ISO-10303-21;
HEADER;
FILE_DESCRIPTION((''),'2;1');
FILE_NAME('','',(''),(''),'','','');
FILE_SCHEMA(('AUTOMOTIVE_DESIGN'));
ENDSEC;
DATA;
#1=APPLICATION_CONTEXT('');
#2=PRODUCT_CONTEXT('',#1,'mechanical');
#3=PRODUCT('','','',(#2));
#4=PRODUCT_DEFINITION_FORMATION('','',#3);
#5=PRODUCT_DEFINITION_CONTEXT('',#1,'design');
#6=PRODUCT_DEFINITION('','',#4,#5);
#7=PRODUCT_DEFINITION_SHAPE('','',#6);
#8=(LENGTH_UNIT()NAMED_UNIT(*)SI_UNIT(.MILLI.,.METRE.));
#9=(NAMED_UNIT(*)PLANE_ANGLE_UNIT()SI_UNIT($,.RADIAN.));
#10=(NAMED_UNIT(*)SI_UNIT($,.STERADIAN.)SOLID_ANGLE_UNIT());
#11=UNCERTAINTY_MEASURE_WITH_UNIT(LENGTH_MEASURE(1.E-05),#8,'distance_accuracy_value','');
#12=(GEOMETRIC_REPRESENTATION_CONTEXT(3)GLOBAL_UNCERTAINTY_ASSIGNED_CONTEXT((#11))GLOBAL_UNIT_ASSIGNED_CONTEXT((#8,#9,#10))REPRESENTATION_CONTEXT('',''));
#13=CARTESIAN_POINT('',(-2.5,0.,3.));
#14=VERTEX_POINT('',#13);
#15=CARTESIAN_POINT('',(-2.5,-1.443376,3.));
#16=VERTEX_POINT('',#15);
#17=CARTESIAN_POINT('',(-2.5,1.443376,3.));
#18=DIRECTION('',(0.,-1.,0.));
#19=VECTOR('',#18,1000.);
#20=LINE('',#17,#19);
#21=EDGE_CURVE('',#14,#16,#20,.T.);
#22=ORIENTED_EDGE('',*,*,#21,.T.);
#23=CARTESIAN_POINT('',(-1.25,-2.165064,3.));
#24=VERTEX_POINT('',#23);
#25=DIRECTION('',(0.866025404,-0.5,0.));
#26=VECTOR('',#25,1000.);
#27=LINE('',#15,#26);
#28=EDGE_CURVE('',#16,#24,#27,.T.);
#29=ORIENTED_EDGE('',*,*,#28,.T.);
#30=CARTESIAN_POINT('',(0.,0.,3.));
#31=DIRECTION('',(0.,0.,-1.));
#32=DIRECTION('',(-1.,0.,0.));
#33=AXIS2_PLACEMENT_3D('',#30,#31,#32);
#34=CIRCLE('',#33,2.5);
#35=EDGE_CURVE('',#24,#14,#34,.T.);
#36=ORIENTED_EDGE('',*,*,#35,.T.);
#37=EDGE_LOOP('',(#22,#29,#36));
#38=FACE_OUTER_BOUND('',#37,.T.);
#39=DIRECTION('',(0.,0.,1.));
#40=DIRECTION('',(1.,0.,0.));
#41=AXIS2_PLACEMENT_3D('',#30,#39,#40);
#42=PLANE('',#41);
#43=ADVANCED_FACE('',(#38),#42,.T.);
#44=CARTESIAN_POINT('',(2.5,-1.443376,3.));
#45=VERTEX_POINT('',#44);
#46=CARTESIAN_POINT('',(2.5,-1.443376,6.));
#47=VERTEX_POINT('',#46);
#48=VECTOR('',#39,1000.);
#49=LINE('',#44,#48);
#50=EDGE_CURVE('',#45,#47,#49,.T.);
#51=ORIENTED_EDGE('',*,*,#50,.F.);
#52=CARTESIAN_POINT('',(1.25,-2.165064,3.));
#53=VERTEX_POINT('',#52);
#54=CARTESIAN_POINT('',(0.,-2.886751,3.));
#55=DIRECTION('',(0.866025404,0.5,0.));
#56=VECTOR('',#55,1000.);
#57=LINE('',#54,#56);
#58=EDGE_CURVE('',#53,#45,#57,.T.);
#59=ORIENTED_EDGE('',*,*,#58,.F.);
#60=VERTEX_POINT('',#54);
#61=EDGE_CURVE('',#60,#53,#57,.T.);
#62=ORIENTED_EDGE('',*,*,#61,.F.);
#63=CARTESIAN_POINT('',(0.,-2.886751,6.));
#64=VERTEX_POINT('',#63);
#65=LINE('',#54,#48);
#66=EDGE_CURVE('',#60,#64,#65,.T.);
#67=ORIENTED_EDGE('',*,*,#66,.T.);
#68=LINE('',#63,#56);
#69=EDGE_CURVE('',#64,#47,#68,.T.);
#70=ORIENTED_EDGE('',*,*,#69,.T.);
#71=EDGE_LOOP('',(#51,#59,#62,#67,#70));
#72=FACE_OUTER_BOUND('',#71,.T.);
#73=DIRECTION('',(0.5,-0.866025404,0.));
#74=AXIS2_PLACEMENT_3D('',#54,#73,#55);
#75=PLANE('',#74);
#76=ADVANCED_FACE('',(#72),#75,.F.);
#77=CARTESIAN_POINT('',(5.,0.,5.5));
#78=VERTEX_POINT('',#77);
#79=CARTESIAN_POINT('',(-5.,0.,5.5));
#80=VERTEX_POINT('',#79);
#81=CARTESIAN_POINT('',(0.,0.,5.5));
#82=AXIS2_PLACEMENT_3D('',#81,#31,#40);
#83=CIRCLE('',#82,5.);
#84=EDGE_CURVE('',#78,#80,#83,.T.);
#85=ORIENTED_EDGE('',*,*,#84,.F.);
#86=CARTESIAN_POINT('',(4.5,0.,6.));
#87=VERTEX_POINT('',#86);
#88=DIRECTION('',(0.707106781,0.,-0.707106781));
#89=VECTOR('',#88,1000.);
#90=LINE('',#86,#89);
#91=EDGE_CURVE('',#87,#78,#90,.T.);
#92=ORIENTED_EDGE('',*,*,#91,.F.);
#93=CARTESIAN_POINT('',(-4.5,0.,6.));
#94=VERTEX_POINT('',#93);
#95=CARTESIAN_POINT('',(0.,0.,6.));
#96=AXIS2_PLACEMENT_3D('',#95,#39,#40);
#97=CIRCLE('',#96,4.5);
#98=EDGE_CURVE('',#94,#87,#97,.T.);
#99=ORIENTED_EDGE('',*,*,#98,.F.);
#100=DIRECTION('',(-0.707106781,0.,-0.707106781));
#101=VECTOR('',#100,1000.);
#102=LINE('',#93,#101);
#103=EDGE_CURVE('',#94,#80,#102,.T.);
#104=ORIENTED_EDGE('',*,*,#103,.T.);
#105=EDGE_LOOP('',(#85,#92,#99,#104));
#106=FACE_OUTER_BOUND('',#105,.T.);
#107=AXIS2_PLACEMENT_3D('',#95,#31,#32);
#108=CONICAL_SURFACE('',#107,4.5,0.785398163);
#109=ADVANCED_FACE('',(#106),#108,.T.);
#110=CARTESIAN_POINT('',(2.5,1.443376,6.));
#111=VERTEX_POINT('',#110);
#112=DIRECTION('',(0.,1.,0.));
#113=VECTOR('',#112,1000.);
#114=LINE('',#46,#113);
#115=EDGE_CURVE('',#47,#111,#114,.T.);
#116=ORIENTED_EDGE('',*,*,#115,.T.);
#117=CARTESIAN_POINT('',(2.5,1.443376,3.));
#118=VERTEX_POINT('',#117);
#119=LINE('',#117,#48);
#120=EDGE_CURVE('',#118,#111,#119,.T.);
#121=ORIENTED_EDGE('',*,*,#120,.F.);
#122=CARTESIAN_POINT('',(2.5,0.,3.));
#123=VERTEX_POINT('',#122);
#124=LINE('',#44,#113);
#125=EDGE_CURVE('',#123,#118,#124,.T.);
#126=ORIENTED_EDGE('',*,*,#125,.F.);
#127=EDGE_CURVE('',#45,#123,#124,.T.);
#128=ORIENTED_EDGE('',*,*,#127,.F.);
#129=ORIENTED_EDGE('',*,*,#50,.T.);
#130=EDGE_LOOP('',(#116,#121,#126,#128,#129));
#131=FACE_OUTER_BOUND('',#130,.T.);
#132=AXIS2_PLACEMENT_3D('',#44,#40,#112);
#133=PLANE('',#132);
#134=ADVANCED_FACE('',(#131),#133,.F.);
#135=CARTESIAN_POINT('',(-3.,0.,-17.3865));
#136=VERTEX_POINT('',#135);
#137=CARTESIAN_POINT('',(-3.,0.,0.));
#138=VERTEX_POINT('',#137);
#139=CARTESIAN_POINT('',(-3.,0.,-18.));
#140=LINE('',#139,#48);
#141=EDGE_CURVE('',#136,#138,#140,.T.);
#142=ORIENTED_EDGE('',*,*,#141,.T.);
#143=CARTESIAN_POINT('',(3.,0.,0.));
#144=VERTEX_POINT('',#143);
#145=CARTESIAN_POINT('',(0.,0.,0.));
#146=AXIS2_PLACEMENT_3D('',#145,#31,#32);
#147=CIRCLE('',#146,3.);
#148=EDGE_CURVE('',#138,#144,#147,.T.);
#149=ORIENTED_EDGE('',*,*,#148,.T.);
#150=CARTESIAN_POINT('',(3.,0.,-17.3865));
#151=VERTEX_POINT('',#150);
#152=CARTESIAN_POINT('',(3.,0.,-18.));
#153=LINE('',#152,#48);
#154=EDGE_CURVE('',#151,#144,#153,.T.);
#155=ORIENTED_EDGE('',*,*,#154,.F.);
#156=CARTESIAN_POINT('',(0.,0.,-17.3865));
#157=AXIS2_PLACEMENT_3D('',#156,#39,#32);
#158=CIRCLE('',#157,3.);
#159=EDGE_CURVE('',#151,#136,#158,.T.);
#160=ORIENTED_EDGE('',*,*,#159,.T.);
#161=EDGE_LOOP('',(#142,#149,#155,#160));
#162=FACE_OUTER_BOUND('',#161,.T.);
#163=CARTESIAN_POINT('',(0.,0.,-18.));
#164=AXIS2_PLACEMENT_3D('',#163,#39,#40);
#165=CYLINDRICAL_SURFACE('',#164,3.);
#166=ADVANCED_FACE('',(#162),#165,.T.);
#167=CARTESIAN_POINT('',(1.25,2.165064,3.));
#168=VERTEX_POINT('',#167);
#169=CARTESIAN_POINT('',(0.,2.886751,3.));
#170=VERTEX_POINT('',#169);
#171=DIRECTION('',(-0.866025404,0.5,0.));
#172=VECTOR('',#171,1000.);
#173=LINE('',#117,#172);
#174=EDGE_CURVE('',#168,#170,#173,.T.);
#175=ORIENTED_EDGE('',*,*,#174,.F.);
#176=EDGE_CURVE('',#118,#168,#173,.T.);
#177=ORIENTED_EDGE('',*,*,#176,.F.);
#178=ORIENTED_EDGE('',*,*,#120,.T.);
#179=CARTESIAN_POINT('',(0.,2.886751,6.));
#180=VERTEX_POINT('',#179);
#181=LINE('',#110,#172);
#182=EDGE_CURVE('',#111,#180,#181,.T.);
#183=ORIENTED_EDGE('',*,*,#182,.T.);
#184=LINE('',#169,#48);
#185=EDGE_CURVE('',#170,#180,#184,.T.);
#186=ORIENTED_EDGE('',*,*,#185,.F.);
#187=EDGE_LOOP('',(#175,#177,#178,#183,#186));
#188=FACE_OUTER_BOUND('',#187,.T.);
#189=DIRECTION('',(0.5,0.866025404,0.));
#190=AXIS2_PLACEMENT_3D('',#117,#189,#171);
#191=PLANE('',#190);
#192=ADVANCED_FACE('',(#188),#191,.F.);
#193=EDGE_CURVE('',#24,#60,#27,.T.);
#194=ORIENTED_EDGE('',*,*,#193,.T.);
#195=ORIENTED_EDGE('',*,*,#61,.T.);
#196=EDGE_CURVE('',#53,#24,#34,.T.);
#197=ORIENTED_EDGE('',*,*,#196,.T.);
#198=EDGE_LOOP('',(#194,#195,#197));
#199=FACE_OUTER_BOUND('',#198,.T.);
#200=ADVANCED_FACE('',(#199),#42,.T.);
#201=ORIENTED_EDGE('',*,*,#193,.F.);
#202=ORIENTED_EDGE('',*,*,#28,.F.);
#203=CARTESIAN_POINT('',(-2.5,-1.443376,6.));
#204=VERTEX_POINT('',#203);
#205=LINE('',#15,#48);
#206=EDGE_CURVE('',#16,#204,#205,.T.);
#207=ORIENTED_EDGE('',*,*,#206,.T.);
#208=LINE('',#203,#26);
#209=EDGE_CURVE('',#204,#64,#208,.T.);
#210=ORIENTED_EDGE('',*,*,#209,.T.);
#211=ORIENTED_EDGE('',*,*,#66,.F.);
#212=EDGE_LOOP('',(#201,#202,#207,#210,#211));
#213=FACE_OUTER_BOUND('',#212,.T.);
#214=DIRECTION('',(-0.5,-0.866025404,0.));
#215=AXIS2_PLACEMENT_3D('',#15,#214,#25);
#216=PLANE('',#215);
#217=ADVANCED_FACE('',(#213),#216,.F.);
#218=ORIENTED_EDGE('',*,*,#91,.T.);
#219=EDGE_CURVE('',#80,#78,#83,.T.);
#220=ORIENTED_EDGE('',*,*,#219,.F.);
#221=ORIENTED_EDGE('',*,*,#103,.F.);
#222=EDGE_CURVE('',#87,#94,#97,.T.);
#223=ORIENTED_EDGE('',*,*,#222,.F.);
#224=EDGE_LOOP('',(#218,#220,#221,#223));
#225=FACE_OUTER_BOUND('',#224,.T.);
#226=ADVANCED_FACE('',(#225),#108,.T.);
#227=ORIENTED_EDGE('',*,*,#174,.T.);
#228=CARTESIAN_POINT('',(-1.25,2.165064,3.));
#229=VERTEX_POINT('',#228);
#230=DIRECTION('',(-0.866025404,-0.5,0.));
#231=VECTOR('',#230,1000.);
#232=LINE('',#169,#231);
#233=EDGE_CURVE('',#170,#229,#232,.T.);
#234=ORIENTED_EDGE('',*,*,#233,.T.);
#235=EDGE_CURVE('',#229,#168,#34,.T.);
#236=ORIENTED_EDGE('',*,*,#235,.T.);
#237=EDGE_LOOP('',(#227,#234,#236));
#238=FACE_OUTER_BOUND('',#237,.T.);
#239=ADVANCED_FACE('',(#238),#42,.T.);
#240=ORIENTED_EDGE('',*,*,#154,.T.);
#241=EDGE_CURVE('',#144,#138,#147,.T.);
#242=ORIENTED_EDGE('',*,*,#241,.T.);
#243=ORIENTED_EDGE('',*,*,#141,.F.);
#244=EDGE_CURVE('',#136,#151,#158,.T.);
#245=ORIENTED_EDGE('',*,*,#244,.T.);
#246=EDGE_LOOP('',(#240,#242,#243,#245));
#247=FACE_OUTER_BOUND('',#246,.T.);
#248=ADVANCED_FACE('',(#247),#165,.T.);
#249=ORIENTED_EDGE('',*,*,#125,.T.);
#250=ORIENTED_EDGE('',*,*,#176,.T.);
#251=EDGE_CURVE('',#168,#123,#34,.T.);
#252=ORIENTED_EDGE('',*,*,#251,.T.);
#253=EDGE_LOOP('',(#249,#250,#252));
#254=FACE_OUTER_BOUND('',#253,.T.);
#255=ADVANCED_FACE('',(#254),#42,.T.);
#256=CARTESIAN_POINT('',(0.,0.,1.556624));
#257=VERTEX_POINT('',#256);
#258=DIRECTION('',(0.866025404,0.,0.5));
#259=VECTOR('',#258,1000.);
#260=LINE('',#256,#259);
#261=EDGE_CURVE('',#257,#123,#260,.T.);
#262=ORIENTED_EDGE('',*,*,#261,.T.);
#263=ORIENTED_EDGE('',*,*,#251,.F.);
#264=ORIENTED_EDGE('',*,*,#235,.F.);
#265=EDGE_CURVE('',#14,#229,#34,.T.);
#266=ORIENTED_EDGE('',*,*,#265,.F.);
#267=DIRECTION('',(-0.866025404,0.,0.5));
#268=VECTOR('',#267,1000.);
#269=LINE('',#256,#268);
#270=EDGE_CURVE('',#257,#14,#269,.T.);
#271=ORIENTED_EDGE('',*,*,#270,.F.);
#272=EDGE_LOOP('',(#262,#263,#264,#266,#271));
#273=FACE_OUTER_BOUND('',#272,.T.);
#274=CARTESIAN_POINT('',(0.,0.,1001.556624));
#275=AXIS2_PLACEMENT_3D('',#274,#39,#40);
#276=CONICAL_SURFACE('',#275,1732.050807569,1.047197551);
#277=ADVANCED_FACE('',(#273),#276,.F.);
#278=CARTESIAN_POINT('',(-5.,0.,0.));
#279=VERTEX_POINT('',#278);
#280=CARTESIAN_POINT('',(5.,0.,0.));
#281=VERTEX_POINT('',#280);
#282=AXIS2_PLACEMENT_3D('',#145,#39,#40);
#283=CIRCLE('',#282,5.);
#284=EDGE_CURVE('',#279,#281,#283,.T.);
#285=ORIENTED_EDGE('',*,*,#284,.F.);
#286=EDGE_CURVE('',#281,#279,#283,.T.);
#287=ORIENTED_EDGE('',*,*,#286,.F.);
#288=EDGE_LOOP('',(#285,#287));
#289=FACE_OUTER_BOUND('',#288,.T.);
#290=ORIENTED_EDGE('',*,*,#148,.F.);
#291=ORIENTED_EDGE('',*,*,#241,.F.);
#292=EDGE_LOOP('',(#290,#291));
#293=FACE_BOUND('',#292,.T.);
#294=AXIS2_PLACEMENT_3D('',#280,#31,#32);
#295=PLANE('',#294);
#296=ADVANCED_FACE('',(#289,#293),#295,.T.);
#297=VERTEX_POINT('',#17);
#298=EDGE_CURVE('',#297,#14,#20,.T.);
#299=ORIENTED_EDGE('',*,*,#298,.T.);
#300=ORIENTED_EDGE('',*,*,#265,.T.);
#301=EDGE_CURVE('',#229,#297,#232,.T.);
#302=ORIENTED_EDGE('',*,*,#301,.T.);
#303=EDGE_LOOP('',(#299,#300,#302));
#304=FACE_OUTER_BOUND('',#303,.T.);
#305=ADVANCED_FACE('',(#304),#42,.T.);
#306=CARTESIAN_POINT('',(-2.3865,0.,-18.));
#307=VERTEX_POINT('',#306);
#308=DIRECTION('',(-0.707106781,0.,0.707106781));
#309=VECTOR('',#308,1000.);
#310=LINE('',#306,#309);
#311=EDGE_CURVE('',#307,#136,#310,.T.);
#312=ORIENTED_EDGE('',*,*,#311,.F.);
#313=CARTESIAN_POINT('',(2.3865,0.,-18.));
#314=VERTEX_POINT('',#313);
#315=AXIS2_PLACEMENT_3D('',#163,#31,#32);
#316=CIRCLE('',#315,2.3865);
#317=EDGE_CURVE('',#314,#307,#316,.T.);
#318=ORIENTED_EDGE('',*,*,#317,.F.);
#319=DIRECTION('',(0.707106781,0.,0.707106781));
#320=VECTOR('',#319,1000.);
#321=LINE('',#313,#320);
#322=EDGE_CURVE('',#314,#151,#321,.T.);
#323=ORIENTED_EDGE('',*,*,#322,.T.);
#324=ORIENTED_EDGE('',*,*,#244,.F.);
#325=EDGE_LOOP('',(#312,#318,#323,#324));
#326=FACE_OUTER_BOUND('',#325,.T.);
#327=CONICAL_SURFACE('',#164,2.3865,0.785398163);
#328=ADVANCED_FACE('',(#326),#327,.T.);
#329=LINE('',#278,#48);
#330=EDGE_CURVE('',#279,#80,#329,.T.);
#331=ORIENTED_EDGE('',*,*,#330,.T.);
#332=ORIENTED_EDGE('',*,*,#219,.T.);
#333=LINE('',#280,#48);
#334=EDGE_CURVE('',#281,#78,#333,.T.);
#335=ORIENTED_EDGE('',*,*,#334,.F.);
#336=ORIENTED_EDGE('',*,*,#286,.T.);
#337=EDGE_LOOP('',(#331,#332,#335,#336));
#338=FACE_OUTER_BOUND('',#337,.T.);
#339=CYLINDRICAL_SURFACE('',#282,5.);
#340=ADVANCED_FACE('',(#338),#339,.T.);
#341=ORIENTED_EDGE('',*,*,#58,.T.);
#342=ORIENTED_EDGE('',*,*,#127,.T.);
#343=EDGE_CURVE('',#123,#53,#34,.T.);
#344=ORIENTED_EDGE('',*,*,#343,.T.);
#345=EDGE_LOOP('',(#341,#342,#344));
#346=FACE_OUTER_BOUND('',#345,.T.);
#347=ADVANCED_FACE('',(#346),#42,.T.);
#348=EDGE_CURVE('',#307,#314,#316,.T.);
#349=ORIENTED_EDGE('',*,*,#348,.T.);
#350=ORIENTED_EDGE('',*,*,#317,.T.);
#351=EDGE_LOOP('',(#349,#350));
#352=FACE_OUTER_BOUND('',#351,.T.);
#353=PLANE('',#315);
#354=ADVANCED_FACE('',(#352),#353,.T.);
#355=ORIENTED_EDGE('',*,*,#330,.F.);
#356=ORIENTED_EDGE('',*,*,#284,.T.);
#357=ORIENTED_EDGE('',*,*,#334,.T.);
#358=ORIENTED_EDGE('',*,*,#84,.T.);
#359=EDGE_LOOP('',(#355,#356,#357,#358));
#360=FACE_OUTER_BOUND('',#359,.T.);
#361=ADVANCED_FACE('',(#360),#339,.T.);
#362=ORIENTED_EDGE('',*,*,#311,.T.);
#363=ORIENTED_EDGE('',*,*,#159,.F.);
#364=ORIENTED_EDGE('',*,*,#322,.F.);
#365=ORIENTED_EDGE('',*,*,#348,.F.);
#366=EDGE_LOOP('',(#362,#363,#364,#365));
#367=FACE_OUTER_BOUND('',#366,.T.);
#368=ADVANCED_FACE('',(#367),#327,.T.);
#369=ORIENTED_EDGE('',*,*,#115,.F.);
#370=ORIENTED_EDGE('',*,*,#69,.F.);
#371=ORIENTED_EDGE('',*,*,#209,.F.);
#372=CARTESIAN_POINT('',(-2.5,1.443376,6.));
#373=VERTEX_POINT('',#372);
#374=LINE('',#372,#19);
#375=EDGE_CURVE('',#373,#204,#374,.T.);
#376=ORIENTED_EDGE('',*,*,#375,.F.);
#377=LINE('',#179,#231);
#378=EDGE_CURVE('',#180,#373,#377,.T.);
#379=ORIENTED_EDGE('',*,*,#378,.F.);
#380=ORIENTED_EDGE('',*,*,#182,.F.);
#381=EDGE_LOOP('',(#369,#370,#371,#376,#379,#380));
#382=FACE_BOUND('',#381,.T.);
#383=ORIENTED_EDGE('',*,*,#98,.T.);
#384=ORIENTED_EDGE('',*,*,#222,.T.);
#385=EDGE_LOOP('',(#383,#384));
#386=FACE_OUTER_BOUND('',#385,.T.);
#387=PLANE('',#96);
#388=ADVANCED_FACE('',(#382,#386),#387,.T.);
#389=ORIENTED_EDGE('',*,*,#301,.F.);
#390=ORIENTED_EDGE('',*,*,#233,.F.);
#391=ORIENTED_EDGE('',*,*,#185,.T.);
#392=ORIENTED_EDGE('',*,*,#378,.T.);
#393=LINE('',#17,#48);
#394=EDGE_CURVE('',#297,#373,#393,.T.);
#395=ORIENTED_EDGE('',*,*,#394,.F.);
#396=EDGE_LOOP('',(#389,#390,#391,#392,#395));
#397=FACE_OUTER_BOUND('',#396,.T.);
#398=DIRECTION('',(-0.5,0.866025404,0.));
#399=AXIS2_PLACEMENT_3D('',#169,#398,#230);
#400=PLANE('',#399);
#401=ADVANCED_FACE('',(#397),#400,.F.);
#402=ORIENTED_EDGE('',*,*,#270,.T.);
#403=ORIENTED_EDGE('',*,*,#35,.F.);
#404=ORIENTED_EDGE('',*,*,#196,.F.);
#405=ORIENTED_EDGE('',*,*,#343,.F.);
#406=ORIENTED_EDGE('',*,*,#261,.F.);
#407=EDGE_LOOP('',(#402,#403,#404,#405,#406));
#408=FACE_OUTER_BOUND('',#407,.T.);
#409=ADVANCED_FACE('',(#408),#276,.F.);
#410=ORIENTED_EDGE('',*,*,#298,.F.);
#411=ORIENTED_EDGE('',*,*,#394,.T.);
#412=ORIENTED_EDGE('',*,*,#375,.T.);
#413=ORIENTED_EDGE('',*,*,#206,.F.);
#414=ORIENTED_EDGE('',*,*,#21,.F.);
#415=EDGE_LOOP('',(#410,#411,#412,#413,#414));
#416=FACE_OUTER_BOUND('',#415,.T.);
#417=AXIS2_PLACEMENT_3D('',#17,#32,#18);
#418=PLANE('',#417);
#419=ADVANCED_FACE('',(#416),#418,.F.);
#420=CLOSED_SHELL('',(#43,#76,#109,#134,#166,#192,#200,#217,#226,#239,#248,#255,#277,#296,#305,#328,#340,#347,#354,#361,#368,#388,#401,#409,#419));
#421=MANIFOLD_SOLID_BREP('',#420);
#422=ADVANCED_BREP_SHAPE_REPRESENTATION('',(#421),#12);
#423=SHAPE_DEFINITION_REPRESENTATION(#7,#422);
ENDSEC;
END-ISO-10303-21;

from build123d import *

# Parameters (mm, degrees)
SKETCH_1_W          = 5
SKETCH_1_H          = 6
SKETCH_2_R          = 3
EXTRUDE_1_DEPTH     = 18
CUT_EXTRUDE_1_DEPTH = 3
CHAMFER_1_SIZE      = 0.5
CHAMFER_2_SIZE      = 0.6135


with BuildPart() as part:
    # 草图1 → 旋转1 (revolve)
    with BuildSketch(Plane(origin=(0, 0, 0), x_dir=(1, 0, 0), z_dir=(0, 1, 0))):
        with Locations((2.5, -3)):
            Rectangle(SKETCH_1_W, SKETCH_1_H)
    revolve(axis=Axis((0, 0, 0), (0, 0, 1)))

    # 草图2 → 凸台-拉伸1 (add)
    with BuildSketch(Plane(origin=(0, 0, 0), x_dir=(-1, 0, 0), z_dir=(0, 0, -1))):
        Circle(SKETCH_2_R)
    extrude(amount=EXTRUDE_1_DEPTH)

    # 草图3 → 切除-拉伸1 (cut)
    with BuildSketch(Plane.XY.offset(6)):
        Polygon((2.5, 1.443375673), (0, 2.886751346), (-2.5, 1.443375673), (-2.5, -1.443375673), (0, -2.886751346), (2.5, -1.443375673), align=None)
    extrude(amount=-CUT_EXTRUDE_1_DEPTH, mode=Mode.SUBTRACT)

    # 草图4 → 切除-旋转1 (revolve, cut)
    with BuildSketch(Plane.XZ):
        Polygon((2.5, 3), (0, 3), (0, 1.556624327), align=None)
    revolve(axis=Axis((0, 0, 3), (0, 0, -1)), mode=Mode.SUBTRACT)

    # 倒角1
    chamfer_1_edges = [part.edges().sort_by_distance(p)[0] for p in [
        (-5, 0, 6),
    ]]
    chamfer(chamfer_1_edges, length=CHAMFER_1_SIZE)

    # 倒角2
    chamfer_2_edges = [part.edges().sort_by_distance(p)[0] for p in [
        (3, 0, -18),
    ]]
    chamfer(chamfer_2_edges, length=CHAMFER_2_SIZE)


solid = part.part
